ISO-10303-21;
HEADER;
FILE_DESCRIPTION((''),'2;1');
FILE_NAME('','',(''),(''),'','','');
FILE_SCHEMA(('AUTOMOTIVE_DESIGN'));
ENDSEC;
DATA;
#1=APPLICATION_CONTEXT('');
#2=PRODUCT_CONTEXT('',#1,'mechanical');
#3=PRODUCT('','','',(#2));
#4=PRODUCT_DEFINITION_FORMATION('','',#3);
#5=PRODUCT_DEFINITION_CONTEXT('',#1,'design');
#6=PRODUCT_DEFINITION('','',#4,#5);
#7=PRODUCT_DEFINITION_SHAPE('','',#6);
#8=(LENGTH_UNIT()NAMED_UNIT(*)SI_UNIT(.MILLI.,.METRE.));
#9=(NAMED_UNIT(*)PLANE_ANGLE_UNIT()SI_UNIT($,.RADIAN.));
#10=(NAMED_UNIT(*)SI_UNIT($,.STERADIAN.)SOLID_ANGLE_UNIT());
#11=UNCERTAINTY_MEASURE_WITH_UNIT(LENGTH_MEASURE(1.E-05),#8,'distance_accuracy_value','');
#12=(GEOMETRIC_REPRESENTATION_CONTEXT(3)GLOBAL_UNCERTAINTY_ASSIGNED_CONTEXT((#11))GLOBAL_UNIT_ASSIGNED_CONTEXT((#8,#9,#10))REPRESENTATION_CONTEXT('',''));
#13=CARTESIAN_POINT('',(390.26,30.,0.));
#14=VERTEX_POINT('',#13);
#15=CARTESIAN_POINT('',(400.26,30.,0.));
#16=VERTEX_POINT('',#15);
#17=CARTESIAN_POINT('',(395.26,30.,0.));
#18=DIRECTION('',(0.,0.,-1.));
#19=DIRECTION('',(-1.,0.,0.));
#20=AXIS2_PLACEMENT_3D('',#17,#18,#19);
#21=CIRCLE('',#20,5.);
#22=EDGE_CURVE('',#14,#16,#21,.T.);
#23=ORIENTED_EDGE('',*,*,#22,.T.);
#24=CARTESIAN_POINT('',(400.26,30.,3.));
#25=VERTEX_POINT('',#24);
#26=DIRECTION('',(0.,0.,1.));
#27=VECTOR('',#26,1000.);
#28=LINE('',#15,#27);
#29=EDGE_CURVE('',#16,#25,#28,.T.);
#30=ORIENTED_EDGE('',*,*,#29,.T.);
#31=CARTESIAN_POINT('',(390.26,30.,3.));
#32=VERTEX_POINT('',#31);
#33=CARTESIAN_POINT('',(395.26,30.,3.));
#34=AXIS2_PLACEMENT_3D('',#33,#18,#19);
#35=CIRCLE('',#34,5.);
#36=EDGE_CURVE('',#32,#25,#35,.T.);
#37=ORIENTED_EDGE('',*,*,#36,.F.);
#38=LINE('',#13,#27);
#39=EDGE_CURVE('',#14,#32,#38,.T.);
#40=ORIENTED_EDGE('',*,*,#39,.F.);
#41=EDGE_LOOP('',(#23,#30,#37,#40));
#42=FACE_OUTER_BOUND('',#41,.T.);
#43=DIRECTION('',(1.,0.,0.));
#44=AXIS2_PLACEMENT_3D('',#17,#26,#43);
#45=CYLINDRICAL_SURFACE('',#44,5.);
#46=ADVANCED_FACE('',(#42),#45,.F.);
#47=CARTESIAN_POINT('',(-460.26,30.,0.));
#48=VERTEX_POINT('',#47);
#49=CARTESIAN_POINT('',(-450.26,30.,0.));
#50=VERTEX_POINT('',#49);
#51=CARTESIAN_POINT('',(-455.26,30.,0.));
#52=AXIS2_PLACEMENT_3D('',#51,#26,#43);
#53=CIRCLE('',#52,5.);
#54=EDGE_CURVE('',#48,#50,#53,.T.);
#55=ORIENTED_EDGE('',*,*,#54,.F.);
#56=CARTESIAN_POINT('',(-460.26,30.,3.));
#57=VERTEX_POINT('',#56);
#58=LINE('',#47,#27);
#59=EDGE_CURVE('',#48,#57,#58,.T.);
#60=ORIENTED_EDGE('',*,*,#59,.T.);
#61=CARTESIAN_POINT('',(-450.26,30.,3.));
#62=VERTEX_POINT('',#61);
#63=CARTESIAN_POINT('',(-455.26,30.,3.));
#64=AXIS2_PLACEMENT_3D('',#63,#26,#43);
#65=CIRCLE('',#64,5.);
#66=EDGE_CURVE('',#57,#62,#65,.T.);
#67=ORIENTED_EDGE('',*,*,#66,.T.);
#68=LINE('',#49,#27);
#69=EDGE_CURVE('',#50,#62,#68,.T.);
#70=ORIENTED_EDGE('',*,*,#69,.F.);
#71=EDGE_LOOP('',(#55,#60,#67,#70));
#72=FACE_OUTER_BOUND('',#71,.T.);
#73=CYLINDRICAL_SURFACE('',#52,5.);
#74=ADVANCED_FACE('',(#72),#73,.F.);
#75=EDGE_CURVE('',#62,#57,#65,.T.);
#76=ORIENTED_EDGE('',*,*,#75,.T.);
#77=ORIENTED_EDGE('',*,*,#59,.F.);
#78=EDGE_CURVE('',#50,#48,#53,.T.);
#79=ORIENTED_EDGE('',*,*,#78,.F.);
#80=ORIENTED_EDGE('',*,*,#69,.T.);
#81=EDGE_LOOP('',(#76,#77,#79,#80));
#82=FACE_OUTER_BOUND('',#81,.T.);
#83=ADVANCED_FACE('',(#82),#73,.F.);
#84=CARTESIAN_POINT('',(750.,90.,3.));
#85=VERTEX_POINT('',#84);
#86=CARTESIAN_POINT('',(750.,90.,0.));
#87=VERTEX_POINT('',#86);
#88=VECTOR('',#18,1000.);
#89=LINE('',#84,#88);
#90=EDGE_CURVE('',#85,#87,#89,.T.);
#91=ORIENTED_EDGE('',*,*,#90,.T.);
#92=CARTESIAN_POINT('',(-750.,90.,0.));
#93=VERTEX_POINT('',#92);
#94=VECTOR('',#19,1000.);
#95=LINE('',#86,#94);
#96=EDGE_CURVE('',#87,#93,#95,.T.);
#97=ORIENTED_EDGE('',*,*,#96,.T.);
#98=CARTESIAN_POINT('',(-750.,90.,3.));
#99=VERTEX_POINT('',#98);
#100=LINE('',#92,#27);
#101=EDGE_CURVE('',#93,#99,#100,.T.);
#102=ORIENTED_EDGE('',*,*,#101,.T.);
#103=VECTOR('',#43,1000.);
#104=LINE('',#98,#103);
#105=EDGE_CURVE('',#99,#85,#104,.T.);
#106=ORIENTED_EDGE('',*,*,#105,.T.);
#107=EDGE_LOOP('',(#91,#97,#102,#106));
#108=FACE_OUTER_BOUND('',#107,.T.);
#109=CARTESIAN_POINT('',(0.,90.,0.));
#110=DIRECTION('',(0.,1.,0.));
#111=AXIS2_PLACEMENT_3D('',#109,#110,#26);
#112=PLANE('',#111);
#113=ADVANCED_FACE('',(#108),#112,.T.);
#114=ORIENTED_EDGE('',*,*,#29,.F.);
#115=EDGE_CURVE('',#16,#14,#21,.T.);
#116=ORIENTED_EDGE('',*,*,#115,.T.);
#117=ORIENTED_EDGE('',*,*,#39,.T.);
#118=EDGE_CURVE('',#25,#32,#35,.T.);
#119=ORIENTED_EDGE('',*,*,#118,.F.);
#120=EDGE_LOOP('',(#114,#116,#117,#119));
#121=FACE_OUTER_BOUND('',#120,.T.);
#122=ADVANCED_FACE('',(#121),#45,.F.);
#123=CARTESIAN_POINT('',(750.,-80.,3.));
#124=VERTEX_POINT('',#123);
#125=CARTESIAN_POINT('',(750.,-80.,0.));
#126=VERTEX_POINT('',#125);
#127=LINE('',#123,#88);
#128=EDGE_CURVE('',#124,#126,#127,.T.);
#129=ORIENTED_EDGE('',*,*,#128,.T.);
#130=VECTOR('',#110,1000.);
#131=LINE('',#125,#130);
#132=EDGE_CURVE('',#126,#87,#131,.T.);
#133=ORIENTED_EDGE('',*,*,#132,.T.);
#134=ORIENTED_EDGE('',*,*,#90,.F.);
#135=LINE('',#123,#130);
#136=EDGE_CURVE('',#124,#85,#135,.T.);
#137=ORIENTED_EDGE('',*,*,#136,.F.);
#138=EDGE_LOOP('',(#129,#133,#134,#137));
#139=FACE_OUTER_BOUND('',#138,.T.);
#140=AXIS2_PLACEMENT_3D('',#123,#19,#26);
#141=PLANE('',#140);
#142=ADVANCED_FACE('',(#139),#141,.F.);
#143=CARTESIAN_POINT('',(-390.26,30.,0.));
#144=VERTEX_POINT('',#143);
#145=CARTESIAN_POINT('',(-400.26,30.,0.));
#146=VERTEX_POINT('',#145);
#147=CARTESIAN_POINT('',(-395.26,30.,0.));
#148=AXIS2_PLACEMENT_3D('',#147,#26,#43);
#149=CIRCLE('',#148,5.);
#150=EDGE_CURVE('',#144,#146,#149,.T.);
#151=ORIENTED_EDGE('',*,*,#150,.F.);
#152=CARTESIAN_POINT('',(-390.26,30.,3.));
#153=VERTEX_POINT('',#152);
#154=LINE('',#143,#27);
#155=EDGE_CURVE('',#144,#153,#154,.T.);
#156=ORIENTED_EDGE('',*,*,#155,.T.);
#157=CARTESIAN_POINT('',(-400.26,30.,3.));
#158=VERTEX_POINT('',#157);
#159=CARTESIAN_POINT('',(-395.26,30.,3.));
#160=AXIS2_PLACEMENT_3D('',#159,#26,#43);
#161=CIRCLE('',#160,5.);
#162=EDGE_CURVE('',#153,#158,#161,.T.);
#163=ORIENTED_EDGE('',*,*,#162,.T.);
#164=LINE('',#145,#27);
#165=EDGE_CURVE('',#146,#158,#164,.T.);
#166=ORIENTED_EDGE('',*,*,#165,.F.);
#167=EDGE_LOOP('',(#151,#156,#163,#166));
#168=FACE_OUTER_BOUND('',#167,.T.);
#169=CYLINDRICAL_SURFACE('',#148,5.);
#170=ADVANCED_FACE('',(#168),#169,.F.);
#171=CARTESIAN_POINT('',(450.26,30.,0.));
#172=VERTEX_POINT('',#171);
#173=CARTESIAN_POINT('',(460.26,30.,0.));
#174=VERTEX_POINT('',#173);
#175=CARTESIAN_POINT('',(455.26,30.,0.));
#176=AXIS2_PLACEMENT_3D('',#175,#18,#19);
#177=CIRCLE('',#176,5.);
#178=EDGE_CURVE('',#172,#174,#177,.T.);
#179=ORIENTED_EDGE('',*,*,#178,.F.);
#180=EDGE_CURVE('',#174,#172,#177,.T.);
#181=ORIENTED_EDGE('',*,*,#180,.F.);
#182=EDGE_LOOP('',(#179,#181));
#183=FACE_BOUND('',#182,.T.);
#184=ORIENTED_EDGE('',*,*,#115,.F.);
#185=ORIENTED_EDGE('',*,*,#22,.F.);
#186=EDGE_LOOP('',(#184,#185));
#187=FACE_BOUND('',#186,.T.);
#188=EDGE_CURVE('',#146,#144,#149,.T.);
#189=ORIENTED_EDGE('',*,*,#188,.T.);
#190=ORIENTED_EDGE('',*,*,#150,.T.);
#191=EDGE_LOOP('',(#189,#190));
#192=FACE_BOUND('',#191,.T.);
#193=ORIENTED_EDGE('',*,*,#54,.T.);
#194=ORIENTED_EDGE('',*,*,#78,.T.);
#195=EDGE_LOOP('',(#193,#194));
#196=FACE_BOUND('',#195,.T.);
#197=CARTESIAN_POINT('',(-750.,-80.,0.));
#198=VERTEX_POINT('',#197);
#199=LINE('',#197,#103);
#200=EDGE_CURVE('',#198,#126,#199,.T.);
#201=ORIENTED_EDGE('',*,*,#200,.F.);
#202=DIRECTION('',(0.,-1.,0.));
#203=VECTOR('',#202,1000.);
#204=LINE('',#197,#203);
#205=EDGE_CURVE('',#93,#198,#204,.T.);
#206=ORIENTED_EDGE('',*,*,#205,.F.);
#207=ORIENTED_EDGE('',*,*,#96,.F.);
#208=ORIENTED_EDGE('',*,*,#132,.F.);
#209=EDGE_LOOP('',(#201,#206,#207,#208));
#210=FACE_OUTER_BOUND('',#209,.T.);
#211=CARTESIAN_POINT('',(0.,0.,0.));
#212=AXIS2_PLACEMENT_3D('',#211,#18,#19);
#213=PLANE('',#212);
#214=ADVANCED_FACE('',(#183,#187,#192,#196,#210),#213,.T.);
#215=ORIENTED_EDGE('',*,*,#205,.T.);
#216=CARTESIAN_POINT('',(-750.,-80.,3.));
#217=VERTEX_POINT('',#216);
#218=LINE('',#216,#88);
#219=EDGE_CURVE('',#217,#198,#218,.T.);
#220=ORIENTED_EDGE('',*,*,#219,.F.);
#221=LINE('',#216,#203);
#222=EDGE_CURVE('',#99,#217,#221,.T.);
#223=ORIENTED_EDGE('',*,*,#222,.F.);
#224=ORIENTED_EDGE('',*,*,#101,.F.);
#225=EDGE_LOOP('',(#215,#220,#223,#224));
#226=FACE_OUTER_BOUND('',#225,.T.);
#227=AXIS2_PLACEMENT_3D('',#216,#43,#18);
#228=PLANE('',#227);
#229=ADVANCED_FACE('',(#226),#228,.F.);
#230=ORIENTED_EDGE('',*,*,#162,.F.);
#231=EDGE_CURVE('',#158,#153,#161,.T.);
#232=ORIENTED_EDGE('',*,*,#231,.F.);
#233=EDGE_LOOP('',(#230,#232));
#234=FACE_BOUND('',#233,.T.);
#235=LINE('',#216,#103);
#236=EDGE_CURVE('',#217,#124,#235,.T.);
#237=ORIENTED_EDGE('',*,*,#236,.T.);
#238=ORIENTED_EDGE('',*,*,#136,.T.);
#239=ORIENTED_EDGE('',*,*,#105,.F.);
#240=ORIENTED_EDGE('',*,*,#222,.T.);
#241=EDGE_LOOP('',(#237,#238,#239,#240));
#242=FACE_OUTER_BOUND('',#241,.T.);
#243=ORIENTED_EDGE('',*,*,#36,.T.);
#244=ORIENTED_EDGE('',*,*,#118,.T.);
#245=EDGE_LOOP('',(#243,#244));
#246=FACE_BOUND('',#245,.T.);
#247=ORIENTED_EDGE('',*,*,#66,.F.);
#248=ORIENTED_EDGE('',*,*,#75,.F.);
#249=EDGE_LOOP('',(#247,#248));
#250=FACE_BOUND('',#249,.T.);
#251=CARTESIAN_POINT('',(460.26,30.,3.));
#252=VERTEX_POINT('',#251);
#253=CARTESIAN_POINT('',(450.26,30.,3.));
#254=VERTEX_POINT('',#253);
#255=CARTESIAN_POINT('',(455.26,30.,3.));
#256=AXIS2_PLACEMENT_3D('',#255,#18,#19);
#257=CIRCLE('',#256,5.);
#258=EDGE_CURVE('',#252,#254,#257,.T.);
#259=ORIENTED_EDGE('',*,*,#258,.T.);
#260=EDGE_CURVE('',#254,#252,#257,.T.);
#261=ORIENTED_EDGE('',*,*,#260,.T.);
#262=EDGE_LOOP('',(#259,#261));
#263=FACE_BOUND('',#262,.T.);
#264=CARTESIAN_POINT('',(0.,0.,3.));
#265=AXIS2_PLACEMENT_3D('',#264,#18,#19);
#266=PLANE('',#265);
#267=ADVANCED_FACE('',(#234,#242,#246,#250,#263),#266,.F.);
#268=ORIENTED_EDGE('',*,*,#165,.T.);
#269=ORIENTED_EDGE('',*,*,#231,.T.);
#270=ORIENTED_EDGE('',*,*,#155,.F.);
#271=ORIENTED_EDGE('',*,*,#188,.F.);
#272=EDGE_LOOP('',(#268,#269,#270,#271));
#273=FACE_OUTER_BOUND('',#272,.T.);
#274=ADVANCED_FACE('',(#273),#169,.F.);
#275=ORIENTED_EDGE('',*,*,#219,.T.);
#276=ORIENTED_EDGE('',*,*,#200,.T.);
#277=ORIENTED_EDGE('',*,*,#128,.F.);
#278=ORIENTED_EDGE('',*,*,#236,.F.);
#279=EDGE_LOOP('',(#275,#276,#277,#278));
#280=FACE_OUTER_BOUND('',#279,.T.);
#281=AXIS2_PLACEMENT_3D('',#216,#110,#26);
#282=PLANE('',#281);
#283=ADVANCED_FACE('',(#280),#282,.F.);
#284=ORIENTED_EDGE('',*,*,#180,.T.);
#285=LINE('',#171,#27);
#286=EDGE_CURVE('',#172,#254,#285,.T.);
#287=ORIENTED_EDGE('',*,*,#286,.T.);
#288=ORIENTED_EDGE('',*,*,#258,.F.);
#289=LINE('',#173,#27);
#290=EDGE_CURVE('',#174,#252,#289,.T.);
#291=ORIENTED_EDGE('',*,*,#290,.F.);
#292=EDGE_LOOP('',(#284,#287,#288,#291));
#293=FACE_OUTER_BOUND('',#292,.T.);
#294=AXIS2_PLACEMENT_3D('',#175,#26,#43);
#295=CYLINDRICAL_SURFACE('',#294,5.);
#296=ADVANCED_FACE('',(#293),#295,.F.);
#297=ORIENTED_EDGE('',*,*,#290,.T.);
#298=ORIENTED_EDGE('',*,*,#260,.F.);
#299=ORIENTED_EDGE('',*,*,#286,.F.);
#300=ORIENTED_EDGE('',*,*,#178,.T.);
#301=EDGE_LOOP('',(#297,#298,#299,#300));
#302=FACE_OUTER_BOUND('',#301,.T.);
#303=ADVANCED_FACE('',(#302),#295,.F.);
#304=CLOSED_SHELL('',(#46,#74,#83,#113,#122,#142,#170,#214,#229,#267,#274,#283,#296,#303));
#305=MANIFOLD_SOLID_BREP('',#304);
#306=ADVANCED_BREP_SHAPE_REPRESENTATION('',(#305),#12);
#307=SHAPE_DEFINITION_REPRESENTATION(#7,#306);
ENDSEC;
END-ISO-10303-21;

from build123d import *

# Parameters (mm, degrees)
SKETCH_1_W          = 1500
SKETCH_1_H          = 160
EXTRUDE_1_DEPTH     = 3
SKETCH_3_R          = 5
CUT_EXTRUDE_1_DEPTH = 755.260565057
SKETCH_7_W          = 1500
SKETCH_7_H          = 3
EXTRUDE_2_DEPTH     = 10


with BuildPart() as part:
    # 草图1 → 凸台-拉伸1 (new body)
    with BuildSketch(Plane.XY):
        Rectangle(SKETCH_1_W, SKETCH_1_H)
    extrude(amount=EXTRUDE_1_DEPTH)

    # 草图3 → 切除-拉伸1 (cut, symmetric)
    with BuildSketch(Plane.XY.offset(3)):
        with Locations((-455.26, 30)):
            Circle(SKETCH_3_R)
        with Locations((-395.26, 30)):
            Circle(SKETCH_3_R)
    cut_extrude_1 = extrude(amount=CUT_EXTRUDE_1_DEPTH, both=True, mode=Mode.SUBTRACT)

    # 镜向1: 切除-拉伸1 across plane
    add(cut_extrude_1.mirror(Plane(origin=(0, 0, 0), x_dir=(0, 0, 1), z_dir=(1, 0, 0))), mode=Mode.SUBTRACT)

    # 草图7 → 凸台-拉伸2 (add)
    with BuildSketch(Plane(origin=(0, 80, 0), x_dir=(1, 0, 0), z_dir=(0, 1, 0))):
        with Locations((0, -1.5)):
            Rectangle(SKETCH_7_W, SKETCH_7_H)
    extrude(amount=EXTRUDE_2_DEPTH)


solid = part.part
